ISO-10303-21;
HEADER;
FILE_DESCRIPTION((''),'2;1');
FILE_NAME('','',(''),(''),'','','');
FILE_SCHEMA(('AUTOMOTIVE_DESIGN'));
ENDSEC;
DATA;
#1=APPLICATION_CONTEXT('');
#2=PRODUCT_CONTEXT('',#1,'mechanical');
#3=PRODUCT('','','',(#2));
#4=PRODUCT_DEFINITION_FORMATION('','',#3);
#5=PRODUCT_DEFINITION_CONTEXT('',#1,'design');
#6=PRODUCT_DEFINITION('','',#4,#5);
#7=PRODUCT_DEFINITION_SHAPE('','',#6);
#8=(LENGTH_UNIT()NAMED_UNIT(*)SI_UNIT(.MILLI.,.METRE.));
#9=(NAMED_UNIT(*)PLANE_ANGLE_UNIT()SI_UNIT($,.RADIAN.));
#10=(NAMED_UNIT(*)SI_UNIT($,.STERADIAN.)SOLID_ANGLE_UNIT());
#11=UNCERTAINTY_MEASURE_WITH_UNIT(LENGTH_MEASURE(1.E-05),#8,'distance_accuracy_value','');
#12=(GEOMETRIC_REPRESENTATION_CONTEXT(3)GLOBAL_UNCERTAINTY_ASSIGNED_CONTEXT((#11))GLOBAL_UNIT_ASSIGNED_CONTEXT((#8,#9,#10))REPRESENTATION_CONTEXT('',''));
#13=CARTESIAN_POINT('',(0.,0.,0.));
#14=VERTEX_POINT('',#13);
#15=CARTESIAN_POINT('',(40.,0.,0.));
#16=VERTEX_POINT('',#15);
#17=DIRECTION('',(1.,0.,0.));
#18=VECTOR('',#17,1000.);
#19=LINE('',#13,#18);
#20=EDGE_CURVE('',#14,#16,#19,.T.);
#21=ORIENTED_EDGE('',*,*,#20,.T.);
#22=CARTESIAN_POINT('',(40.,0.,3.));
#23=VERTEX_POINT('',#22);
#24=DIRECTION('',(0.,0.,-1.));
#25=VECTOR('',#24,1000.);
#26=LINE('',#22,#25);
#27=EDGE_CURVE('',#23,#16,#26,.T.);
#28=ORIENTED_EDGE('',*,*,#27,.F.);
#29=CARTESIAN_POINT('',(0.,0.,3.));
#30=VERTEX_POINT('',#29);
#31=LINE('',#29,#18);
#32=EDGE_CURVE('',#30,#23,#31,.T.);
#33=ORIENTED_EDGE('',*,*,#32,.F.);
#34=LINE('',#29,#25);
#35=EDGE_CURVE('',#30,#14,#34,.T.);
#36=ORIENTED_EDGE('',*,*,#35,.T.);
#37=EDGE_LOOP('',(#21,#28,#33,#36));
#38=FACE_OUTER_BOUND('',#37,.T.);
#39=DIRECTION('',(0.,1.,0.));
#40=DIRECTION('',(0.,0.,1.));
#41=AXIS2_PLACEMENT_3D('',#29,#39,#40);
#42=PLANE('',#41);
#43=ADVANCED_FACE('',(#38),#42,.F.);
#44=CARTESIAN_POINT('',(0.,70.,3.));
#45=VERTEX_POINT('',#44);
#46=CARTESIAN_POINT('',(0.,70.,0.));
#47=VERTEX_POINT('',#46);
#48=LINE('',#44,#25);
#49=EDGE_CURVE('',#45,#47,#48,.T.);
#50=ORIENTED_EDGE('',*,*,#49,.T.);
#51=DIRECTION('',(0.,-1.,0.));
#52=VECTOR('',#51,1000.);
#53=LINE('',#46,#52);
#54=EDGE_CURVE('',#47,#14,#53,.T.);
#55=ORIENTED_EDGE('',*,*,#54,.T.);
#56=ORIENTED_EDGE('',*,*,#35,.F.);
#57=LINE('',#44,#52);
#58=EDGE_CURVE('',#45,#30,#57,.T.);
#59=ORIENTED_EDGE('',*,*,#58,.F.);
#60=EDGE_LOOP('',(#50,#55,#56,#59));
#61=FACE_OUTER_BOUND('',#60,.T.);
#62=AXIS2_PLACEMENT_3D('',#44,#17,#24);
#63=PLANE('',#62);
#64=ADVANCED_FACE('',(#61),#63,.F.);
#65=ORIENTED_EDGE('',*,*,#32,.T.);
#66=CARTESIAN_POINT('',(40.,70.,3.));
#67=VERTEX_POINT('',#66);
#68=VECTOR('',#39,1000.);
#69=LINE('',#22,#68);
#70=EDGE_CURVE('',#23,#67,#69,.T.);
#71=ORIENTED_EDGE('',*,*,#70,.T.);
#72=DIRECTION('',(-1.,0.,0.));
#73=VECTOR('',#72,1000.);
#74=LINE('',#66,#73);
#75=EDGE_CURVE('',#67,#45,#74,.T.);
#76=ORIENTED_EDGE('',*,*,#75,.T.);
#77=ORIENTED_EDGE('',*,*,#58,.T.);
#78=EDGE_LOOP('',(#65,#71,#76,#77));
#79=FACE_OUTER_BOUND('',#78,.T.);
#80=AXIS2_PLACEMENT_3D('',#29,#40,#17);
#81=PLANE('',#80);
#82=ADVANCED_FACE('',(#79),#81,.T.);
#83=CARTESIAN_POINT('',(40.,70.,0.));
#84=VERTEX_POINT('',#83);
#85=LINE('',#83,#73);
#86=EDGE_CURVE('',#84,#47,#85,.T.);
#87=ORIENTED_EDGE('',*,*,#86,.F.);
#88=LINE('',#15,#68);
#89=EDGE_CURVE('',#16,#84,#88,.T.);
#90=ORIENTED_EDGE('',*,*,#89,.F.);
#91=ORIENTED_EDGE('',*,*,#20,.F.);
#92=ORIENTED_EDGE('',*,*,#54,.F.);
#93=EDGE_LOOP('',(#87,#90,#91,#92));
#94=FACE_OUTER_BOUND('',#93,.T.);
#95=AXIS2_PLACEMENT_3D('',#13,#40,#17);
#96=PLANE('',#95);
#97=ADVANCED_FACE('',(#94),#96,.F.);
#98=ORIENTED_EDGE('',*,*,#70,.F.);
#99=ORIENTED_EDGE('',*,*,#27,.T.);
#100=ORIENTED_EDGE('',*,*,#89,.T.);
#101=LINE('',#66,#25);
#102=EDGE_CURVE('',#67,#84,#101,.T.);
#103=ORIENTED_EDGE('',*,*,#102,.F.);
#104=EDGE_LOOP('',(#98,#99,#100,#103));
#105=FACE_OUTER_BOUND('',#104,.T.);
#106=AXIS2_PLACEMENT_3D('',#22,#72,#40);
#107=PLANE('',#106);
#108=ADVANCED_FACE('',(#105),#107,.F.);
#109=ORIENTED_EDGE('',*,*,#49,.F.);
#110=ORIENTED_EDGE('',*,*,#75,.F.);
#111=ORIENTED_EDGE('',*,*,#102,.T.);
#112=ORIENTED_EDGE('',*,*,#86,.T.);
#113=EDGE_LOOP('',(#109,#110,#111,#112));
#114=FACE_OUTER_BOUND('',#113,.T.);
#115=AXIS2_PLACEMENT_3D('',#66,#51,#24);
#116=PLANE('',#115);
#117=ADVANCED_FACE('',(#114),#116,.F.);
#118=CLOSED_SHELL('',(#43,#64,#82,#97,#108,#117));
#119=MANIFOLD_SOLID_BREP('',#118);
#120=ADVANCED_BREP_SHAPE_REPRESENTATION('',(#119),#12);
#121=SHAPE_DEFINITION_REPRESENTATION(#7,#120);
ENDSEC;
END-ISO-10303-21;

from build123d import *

# Parameters (mm, degrees)
SKETCH_1_W      = 40
SKETCH_1_H      = 70
EXTRUDE_1_DEPTH = 3


with BuildPart() as part:
    # 草图1 → 凸台-拉伸1 (new body)
    with BuildSketch(Plane.XY):
        with Locations((20, 35)):
            Rectangle(SKETCH_1_W, SKETCH_1_H)
    extrude(amount=EXTRUDE_1_DEPTH)


solid = part.part
